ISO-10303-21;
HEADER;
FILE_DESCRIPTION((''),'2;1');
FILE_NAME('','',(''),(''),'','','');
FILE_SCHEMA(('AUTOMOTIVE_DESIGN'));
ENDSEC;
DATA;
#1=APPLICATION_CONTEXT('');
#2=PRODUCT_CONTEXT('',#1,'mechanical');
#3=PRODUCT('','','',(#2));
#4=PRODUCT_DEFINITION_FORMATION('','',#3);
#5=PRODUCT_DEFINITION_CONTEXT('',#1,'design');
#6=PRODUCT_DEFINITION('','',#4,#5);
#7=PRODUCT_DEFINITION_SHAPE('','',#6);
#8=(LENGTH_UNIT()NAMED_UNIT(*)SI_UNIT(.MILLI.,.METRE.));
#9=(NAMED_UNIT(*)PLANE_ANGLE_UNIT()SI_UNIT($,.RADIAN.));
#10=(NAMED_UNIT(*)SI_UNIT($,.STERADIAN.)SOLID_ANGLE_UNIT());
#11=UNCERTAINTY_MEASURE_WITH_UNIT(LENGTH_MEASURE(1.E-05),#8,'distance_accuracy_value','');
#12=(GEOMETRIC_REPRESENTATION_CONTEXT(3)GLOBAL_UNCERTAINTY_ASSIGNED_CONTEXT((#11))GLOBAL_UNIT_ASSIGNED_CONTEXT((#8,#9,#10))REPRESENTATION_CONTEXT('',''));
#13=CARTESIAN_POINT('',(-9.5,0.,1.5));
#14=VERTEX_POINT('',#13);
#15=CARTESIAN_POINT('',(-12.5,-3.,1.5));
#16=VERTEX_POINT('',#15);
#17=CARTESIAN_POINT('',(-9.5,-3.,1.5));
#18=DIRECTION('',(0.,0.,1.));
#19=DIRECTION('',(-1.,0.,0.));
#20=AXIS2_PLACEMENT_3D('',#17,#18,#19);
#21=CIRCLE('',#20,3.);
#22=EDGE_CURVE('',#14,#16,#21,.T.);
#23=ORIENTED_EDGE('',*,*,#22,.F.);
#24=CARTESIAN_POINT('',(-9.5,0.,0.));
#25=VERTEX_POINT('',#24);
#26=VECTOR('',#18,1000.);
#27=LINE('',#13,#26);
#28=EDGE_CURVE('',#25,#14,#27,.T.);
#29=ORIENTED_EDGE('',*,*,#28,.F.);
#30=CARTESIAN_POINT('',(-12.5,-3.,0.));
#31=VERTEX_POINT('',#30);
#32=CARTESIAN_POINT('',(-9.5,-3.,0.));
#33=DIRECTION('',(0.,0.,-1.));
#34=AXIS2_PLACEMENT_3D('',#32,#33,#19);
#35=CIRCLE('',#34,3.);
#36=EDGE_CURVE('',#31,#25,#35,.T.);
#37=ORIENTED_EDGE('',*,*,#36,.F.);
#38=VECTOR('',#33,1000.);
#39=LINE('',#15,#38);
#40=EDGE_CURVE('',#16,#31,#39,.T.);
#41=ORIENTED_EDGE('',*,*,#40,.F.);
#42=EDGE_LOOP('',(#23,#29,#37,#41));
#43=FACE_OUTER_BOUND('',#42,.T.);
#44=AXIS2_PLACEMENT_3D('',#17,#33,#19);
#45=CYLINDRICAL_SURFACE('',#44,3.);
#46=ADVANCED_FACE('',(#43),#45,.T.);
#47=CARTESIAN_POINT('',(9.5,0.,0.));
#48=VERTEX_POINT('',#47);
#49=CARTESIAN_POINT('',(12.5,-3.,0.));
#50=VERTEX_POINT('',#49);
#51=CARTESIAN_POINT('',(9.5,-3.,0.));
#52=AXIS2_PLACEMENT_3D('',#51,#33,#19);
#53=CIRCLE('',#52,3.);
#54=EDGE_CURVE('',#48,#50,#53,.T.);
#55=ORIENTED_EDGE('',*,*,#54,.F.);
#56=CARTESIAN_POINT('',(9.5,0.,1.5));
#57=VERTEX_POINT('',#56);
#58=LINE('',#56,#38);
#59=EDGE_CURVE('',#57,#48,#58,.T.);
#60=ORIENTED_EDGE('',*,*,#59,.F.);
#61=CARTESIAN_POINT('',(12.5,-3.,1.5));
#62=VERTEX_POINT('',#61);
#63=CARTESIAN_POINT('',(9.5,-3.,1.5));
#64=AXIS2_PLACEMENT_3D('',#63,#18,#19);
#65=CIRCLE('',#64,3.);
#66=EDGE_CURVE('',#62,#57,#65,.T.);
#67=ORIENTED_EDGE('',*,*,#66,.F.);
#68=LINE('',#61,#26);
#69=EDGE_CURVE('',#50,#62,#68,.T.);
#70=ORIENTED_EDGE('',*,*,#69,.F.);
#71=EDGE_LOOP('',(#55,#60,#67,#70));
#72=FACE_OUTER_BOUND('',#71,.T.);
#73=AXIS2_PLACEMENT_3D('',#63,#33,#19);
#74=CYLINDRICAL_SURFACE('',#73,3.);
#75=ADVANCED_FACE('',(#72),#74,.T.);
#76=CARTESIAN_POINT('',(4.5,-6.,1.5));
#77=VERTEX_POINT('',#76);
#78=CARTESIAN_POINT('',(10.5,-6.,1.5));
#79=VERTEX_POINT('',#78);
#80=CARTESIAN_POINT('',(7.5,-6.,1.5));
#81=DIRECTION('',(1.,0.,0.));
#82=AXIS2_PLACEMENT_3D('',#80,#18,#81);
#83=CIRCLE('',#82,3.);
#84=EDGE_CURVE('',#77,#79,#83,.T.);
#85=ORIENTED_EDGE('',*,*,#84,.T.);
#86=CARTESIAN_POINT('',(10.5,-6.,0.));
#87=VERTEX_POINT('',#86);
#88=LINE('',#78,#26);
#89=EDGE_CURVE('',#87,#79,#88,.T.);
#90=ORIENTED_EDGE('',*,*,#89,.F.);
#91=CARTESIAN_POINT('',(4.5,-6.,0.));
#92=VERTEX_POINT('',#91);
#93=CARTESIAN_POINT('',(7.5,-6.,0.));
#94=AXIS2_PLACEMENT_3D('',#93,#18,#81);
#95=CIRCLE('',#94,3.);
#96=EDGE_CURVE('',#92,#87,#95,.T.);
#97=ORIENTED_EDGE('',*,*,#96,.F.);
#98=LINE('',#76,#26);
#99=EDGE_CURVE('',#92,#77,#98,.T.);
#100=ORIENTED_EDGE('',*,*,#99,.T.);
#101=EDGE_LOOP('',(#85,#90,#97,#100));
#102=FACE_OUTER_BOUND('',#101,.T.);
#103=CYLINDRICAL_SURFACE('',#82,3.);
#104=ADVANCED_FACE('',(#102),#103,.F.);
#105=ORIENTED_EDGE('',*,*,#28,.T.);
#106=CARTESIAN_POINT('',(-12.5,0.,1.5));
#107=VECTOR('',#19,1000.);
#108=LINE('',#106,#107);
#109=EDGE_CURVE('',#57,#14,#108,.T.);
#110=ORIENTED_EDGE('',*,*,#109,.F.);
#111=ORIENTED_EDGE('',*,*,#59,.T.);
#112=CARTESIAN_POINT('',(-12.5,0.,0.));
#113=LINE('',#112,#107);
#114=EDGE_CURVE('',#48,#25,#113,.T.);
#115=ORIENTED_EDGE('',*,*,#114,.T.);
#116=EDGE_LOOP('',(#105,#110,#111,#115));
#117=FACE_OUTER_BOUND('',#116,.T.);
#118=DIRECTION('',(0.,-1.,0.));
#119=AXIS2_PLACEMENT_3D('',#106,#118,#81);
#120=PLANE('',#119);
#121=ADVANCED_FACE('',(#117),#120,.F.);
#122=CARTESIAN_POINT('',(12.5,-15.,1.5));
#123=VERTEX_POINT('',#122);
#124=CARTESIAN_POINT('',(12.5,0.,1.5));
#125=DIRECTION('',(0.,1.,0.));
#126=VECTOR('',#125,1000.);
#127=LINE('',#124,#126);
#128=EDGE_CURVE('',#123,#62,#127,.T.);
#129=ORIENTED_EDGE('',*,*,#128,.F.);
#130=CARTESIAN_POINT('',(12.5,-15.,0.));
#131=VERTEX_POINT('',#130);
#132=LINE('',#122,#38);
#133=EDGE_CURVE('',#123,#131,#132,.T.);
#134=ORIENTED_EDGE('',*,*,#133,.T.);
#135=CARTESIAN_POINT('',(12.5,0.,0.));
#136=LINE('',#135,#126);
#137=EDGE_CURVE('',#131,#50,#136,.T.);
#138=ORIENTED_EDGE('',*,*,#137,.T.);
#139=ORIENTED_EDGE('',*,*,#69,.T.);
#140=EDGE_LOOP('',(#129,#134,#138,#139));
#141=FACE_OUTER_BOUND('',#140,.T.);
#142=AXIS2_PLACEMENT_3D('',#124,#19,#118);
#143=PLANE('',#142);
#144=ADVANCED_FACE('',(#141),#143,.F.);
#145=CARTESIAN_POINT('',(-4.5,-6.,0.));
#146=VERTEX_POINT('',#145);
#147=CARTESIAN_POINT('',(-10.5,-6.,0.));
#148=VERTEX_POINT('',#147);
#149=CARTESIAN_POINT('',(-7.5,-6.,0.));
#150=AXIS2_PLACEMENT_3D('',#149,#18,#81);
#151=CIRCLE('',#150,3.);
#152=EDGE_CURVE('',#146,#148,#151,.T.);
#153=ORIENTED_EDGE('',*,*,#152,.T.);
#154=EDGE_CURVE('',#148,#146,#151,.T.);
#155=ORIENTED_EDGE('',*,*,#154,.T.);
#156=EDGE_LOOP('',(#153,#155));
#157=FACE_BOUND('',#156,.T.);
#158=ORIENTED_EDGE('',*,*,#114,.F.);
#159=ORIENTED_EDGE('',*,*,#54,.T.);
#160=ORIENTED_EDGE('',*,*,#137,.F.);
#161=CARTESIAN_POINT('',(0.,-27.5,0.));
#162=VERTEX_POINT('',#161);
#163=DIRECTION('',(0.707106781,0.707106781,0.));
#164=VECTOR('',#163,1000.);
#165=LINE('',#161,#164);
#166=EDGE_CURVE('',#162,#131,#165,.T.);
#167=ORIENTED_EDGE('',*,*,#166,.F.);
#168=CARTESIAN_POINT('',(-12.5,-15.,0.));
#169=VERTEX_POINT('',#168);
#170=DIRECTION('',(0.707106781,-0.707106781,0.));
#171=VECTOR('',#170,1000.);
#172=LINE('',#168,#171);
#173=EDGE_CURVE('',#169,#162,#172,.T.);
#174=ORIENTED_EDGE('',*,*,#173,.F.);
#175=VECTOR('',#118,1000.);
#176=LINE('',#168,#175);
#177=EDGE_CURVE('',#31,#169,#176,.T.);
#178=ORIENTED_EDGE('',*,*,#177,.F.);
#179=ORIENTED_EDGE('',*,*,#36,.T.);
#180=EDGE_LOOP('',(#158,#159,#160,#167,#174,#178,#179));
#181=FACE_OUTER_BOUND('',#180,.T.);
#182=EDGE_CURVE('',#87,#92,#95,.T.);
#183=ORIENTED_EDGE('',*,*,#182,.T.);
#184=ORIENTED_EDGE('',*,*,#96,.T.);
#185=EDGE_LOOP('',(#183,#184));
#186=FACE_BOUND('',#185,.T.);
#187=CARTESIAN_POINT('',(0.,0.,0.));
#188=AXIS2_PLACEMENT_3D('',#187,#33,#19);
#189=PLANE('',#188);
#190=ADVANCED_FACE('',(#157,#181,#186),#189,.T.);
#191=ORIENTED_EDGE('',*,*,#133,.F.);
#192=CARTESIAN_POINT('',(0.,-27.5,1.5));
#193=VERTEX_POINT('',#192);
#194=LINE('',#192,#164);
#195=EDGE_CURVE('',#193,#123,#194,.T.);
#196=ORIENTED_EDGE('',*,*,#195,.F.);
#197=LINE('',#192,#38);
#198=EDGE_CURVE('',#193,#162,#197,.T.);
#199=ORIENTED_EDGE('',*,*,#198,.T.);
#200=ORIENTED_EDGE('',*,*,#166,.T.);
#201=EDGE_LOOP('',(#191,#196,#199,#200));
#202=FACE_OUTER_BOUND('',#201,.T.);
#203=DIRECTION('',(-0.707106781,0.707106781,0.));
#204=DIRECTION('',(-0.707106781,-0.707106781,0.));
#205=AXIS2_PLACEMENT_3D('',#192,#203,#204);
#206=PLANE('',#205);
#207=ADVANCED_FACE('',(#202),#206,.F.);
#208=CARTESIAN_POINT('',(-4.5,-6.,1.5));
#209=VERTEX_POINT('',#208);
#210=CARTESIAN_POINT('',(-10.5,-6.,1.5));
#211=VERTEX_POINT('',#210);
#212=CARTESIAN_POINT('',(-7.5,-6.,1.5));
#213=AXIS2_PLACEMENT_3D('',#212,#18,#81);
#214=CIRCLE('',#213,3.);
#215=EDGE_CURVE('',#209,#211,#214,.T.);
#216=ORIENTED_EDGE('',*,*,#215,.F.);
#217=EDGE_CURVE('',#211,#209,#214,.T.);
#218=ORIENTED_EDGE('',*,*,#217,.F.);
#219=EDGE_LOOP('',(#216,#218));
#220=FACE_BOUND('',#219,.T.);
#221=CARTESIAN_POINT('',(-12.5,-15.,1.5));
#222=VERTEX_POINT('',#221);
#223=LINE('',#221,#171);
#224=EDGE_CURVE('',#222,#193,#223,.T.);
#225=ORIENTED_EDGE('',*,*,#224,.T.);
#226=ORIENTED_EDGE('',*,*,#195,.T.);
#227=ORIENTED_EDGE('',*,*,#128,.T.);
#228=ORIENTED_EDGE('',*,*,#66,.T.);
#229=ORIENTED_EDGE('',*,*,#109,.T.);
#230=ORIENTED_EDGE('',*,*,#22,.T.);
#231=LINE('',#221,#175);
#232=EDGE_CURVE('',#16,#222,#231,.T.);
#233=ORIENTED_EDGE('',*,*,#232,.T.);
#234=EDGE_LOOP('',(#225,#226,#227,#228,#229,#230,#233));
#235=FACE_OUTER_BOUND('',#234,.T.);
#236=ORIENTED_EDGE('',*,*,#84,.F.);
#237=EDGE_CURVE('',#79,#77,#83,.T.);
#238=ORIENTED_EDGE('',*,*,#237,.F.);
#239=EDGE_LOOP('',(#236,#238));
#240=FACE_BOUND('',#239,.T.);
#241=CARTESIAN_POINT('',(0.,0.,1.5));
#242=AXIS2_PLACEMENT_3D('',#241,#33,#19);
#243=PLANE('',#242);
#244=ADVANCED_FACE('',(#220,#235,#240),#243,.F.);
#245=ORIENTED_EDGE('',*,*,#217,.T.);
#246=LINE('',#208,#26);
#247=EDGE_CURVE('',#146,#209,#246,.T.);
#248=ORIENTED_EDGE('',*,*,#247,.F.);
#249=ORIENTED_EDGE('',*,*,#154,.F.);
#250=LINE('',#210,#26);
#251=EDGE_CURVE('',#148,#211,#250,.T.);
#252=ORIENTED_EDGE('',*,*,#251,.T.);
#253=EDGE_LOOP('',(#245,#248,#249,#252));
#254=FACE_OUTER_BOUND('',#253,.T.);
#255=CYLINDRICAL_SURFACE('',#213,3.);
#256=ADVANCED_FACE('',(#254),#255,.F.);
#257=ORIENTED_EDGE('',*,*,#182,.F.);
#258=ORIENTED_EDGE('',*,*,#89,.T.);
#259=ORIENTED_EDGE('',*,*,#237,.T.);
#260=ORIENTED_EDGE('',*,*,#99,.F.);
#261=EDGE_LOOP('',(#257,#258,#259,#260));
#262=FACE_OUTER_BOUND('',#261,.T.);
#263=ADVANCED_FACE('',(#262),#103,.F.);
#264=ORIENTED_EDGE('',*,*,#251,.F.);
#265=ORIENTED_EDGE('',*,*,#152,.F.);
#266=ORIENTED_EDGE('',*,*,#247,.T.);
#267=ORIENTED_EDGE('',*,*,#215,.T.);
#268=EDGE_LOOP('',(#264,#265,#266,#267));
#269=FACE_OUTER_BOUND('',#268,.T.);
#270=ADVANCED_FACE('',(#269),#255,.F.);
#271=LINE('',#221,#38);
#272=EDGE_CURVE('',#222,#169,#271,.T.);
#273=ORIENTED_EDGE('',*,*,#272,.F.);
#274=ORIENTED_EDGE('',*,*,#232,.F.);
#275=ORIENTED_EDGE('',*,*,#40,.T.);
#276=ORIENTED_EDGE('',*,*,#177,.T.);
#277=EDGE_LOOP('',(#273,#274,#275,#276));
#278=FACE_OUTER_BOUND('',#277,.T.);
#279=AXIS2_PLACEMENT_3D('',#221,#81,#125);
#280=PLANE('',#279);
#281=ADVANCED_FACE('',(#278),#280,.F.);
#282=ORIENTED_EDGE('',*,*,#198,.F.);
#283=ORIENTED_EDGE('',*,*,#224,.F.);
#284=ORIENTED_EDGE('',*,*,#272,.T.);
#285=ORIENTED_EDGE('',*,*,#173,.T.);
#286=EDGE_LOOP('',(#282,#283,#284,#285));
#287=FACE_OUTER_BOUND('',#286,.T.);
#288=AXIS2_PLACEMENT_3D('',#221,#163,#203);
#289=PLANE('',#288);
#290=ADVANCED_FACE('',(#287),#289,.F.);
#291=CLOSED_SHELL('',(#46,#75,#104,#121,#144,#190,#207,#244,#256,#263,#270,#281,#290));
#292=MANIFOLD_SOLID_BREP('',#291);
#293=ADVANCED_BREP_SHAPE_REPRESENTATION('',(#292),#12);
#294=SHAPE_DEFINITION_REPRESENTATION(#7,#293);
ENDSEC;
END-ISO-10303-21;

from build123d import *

# Parameters (mm, degrees)
EXTRUDE_1_DEPTH       = 1.5
HOLE_WIZARD_6_0_6_1_D = 6
FILLET_1_R            = 3


with BuildPart() as part:
    # 草图1 → 凸台-拉伸1 (new body)
    with BuildSketch(Plane.XY):
        Polygon((-12.5, 0), (12.5, 0), (12.5, -15), (0, -27.5), (-12.5, -15), align=None)
    extrude(amount=EXTRUDE_1_DEPTH)

    # Ø6.0 (6) 直径孔1 (through all)
    with Locations(Plane.XY.offset(1.5)):
        with Locations((-7.5, -6), (7.5, -6)):
            Hole(HOLE_WIZARD_6_0_6_1_D / 2)

    # 圆角1
    fillet_1_edges = [part.edges().sort_by_distance(p)[0] for p in [
        (-12.5, 0, 0.75),
        (12.5, 0, 0.75),
    ]]
    fillet(fillet_1_edges, radius=FILLET_1_R)


solid = part.part
